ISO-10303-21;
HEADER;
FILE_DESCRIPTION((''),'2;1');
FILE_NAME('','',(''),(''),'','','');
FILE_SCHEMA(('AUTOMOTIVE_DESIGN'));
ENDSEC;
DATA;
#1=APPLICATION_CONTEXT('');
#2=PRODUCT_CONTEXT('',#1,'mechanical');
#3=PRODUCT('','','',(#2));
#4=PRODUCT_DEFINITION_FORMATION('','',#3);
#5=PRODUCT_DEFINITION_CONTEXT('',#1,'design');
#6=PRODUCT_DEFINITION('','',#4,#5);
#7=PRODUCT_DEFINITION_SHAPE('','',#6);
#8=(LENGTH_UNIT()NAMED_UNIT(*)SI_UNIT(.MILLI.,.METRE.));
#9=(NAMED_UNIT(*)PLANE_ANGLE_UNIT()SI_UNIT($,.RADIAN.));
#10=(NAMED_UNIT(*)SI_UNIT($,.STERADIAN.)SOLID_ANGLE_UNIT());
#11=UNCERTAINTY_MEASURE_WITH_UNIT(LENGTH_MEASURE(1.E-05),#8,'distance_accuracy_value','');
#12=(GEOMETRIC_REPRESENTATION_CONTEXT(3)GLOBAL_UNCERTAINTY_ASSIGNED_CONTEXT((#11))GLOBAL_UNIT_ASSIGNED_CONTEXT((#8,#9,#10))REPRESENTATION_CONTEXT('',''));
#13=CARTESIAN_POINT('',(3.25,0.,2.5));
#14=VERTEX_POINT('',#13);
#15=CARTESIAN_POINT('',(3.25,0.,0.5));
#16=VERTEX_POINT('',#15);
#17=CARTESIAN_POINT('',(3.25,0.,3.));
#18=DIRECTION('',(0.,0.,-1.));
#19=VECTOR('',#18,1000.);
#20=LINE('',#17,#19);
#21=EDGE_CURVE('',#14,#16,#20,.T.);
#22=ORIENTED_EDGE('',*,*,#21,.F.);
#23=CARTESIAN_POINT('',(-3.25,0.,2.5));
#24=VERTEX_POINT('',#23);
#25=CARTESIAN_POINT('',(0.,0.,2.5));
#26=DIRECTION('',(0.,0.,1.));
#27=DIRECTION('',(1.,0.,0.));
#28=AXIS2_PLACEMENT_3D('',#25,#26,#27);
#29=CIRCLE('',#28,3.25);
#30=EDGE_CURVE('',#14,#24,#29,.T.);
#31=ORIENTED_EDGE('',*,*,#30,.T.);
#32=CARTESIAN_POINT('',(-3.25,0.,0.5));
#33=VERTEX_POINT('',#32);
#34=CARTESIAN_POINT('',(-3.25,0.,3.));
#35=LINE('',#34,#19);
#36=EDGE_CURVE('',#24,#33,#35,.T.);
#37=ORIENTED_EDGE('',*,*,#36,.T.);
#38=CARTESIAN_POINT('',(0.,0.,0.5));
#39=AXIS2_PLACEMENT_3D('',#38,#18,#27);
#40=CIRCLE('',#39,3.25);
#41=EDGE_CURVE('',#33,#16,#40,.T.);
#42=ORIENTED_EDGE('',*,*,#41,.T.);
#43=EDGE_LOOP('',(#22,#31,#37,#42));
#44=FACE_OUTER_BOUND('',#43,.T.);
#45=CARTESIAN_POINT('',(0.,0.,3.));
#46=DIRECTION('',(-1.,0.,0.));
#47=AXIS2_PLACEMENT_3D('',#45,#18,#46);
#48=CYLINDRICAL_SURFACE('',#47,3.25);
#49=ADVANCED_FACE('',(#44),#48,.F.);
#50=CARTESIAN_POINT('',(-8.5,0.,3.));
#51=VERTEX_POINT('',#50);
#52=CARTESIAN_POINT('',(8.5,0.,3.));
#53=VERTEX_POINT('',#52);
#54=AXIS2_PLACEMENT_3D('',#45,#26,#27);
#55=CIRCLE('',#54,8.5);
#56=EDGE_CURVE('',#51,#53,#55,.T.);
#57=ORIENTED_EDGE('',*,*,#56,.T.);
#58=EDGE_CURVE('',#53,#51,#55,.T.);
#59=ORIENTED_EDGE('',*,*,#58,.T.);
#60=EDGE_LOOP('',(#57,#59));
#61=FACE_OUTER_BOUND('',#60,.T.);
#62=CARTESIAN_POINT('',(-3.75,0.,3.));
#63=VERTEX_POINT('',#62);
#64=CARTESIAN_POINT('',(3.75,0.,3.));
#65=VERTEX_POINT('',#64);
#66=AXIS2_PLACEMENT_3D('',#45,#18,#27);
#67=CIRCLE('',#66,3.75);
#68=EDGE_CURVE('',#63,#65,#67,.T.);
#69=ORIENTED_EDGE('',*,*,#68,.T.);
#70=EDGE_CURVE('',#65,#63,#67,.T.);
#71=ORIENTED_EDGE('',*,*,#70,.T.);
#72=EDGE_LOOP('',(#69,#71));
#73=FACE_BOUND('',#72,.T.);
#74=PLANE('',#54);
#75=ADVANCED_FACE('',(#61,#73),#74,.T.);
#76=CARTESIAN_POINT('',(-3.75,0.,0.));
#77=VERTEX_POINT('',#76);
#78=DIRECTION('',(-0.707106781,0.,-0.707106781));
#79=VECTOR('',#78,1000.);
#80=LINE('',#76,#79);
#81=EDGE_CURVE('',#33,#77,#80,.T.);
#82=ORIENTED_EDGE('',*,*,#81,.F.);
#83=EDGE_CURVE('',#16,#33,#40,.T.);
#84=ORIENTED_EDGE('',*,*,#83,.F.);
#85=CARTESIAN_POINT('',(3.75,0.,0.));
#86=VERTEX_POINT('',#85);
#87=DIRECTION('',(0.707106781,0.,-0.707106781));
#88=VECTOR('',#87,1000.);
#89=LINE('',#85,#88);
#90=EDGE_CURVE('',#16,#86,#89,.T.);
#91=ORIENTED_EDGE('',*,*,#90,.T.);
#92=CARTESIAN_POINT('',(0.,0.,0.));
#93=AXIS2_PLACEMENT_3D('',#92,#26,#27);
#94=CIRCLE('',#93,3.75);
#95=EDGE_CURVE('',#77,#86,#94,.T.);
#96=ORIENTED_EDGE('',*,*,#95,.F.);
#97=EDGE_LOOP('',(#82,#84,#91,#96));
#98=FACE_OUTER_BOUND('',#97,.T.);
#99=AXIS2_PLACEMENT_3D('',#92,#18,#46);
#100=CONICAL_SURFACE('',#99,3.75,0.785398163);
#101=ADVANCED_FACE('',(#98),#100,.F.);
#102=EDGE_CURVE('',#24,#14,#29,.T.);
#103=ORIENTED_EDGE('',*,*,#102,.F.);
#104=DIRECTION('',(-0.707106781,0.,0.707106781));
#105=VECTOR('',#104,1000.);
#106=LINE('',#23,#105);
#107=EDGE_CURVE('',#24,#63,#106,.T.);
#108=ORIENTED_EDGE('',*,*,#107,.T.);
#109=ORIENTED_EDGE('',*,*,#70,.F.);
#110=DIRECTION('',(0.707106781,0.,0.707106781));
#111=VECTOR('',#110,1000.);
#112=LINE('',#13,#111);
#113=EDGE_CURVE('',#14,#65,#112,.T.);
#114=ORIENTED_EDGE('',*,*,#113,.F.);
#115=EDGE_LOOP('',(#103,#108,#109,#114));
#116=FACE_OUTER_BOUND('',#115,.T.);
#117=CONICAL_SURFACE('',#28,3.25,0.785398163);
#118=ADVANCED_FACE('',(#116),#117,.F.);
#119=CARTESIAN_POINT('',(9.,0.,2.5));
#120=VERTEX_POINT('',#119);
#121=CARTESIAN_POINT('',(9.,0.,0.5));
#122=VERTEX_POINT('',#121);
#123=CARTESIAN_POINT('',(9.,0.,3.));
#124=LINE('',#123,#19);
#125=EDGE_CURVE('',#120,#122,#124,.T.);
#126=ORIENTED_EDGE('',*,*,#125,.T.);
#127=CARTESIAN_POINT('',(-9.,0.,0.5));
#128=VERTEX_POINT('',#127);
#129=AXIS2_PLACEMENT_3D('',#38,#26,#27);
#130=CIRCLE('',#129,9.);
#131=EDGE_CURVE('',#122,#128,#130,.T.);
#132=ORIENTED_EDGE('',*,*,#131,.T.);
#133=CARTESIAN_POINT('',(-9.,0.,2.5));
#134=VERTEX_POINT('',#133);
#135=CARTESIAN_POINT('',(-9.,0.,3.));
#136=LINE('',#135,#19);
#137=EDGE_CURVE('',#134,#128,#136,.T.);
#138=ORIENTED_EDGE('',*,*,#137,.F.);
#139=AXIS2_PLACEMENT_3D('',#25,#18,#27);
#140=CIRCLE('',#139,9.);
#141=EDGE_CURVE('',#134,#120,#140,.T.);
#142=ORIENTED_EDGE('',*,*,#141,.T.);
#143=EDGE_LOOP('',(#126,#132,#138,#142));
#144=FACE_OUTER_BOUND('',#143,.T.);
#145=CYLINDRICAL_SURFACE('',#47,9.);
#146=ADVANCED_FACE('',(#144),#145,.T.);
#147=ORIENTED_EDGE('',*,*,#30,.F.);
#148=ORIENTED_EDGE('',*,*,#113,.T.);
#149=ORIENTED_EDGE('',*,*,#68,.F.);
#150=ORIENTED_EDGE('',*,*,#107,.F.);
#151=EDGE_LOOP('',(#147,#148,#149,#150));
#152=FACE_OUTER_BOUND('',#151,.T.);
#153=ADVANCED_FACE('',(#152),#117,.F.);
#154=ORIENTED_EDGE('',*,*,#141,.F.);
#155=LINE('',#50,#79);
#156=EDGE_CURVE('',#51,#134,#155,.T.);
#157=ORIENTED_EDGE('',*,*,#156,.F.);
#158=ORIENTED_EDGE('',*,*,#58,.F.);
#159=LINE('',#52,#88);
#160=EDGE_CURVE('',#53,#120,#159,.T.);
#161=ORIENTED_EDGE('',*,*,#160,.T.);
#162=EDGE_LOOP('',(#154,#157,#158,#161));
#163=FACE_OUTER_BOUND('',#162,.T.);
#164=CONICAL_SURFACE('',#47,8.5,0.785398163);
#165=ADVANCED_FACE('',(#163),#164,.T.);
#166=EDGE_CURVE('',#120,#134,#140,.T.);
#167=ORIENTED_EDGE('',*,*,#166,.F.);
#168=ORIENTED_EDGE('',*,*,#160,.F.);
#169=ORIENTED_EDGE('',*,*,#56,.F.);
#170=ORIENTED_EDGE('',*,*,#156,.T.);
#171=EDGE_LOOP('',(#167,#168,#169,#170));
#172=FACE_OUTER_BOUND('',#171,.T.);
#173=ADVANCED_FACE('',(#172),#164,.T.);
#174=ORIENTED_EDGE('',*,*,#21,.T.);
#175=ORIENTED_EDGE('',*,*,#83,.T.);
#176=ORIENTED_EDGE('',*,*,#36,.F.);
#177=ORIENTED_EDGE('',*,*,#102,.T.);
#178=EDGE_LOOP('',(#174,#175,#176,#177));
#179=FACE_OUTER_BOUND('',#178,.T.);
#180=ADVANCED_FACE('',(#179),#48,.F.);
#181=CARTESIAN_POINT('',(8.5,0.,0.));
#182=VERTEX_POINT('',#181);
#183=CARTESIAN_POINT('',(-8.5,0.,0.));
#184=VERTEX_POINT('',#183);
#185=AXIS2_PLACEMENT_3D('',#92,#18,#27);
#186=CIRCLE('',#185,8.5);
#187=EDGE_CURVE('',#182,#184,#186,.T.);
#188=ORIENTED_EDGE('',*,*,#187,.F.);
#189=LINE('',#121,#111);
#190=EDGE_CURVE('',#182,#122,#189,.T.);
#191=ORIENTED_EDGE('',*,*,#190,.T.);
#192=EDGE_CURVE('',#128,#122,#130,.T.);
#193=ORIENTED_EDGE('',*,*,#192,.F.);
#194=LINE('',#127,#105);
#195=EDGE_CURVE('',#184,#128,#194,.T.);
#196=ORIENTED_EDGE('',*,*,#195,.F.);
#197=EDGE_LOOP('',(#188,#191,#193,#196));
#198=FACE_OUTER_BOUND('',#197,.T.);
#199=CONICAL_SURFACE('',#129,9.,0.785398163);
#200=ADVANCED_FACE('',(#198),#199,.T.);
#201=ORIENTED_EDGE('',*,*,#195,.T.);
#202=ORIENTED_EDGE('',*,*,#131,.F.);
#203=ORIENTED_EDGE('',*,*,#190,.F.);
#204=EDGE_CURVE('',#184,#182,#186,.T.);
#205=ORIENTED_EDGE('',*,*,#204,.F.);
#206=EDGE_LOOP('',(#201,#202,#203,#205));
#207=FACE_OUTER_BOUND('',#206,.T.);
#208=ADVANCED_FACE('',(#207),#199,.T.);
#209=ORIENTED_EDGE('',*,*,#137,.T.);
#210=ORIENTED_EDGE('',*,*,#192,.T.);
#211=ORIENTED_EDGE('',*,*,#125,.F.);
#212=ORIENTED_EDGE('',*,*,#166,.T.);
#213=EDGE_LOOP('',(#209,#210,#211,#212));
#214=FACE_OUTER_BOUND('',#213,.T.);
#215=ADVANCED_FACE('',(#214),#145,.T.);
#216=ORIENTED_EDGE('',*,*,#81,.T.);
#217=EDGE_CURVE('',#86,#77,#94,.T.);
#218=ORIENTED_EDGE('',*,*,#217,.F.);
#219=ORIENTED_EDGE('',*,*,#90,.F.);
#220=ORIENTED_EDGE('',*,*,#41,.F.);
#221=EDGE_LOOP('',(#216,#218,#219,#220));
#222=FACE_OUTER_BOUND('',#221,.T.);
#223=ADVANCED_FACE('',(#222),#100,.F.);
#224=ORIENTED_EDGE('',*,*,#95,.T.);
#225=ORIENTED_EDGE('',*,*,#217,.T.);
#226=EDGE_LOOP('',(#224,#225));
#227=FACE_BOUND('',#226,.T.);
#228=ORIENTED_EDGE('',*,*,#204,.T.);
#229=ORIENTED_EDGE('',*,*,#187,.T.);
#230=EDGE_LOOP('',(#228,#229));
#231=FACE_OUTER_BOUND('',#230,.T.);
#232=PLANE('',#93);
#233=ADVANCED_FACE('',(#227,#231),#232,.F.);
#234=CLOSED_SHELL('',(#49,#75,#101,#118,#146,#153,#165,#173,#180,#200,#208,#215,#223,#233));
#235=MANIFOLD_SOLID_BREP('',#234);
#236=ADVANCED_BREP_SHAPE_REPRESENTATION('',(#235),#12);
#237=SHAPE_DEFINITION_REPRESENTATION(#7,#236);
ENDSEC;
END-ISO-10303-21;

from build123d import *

# Parameters (mm, degrees)
SKETCH1_R           = 9
SKETCH1_R_2         = 3.25
BOSS_EXTRUDE1_DEPTH = 3
CHAMFER1_SIZE       = 0.5


with BuildPart() as part:
    # Sketch1 → Boss-Extrude1 (new body)
    with BuildSketch(Plane.XY):
        Circle(SKETCH1_R)
        Circle(SKETCH1_R_2, mode=Mode.SUBTRACT)
    extrude(amount=BOSS_EXTRUDE1_DEPTH)

    # Chamfer1
    chamfer1_edges = [part.edges().sort_by_distance(p)[0] for p in [
        (-9, 0, 0),
        (-9, 0, 3),
        (-3.25, 0, 0),
        (-3.25, 0, 3),
    ]]
    chamfer(chamfer1_edges, length=CHAMFER1_SIZE)


solid = part.part
